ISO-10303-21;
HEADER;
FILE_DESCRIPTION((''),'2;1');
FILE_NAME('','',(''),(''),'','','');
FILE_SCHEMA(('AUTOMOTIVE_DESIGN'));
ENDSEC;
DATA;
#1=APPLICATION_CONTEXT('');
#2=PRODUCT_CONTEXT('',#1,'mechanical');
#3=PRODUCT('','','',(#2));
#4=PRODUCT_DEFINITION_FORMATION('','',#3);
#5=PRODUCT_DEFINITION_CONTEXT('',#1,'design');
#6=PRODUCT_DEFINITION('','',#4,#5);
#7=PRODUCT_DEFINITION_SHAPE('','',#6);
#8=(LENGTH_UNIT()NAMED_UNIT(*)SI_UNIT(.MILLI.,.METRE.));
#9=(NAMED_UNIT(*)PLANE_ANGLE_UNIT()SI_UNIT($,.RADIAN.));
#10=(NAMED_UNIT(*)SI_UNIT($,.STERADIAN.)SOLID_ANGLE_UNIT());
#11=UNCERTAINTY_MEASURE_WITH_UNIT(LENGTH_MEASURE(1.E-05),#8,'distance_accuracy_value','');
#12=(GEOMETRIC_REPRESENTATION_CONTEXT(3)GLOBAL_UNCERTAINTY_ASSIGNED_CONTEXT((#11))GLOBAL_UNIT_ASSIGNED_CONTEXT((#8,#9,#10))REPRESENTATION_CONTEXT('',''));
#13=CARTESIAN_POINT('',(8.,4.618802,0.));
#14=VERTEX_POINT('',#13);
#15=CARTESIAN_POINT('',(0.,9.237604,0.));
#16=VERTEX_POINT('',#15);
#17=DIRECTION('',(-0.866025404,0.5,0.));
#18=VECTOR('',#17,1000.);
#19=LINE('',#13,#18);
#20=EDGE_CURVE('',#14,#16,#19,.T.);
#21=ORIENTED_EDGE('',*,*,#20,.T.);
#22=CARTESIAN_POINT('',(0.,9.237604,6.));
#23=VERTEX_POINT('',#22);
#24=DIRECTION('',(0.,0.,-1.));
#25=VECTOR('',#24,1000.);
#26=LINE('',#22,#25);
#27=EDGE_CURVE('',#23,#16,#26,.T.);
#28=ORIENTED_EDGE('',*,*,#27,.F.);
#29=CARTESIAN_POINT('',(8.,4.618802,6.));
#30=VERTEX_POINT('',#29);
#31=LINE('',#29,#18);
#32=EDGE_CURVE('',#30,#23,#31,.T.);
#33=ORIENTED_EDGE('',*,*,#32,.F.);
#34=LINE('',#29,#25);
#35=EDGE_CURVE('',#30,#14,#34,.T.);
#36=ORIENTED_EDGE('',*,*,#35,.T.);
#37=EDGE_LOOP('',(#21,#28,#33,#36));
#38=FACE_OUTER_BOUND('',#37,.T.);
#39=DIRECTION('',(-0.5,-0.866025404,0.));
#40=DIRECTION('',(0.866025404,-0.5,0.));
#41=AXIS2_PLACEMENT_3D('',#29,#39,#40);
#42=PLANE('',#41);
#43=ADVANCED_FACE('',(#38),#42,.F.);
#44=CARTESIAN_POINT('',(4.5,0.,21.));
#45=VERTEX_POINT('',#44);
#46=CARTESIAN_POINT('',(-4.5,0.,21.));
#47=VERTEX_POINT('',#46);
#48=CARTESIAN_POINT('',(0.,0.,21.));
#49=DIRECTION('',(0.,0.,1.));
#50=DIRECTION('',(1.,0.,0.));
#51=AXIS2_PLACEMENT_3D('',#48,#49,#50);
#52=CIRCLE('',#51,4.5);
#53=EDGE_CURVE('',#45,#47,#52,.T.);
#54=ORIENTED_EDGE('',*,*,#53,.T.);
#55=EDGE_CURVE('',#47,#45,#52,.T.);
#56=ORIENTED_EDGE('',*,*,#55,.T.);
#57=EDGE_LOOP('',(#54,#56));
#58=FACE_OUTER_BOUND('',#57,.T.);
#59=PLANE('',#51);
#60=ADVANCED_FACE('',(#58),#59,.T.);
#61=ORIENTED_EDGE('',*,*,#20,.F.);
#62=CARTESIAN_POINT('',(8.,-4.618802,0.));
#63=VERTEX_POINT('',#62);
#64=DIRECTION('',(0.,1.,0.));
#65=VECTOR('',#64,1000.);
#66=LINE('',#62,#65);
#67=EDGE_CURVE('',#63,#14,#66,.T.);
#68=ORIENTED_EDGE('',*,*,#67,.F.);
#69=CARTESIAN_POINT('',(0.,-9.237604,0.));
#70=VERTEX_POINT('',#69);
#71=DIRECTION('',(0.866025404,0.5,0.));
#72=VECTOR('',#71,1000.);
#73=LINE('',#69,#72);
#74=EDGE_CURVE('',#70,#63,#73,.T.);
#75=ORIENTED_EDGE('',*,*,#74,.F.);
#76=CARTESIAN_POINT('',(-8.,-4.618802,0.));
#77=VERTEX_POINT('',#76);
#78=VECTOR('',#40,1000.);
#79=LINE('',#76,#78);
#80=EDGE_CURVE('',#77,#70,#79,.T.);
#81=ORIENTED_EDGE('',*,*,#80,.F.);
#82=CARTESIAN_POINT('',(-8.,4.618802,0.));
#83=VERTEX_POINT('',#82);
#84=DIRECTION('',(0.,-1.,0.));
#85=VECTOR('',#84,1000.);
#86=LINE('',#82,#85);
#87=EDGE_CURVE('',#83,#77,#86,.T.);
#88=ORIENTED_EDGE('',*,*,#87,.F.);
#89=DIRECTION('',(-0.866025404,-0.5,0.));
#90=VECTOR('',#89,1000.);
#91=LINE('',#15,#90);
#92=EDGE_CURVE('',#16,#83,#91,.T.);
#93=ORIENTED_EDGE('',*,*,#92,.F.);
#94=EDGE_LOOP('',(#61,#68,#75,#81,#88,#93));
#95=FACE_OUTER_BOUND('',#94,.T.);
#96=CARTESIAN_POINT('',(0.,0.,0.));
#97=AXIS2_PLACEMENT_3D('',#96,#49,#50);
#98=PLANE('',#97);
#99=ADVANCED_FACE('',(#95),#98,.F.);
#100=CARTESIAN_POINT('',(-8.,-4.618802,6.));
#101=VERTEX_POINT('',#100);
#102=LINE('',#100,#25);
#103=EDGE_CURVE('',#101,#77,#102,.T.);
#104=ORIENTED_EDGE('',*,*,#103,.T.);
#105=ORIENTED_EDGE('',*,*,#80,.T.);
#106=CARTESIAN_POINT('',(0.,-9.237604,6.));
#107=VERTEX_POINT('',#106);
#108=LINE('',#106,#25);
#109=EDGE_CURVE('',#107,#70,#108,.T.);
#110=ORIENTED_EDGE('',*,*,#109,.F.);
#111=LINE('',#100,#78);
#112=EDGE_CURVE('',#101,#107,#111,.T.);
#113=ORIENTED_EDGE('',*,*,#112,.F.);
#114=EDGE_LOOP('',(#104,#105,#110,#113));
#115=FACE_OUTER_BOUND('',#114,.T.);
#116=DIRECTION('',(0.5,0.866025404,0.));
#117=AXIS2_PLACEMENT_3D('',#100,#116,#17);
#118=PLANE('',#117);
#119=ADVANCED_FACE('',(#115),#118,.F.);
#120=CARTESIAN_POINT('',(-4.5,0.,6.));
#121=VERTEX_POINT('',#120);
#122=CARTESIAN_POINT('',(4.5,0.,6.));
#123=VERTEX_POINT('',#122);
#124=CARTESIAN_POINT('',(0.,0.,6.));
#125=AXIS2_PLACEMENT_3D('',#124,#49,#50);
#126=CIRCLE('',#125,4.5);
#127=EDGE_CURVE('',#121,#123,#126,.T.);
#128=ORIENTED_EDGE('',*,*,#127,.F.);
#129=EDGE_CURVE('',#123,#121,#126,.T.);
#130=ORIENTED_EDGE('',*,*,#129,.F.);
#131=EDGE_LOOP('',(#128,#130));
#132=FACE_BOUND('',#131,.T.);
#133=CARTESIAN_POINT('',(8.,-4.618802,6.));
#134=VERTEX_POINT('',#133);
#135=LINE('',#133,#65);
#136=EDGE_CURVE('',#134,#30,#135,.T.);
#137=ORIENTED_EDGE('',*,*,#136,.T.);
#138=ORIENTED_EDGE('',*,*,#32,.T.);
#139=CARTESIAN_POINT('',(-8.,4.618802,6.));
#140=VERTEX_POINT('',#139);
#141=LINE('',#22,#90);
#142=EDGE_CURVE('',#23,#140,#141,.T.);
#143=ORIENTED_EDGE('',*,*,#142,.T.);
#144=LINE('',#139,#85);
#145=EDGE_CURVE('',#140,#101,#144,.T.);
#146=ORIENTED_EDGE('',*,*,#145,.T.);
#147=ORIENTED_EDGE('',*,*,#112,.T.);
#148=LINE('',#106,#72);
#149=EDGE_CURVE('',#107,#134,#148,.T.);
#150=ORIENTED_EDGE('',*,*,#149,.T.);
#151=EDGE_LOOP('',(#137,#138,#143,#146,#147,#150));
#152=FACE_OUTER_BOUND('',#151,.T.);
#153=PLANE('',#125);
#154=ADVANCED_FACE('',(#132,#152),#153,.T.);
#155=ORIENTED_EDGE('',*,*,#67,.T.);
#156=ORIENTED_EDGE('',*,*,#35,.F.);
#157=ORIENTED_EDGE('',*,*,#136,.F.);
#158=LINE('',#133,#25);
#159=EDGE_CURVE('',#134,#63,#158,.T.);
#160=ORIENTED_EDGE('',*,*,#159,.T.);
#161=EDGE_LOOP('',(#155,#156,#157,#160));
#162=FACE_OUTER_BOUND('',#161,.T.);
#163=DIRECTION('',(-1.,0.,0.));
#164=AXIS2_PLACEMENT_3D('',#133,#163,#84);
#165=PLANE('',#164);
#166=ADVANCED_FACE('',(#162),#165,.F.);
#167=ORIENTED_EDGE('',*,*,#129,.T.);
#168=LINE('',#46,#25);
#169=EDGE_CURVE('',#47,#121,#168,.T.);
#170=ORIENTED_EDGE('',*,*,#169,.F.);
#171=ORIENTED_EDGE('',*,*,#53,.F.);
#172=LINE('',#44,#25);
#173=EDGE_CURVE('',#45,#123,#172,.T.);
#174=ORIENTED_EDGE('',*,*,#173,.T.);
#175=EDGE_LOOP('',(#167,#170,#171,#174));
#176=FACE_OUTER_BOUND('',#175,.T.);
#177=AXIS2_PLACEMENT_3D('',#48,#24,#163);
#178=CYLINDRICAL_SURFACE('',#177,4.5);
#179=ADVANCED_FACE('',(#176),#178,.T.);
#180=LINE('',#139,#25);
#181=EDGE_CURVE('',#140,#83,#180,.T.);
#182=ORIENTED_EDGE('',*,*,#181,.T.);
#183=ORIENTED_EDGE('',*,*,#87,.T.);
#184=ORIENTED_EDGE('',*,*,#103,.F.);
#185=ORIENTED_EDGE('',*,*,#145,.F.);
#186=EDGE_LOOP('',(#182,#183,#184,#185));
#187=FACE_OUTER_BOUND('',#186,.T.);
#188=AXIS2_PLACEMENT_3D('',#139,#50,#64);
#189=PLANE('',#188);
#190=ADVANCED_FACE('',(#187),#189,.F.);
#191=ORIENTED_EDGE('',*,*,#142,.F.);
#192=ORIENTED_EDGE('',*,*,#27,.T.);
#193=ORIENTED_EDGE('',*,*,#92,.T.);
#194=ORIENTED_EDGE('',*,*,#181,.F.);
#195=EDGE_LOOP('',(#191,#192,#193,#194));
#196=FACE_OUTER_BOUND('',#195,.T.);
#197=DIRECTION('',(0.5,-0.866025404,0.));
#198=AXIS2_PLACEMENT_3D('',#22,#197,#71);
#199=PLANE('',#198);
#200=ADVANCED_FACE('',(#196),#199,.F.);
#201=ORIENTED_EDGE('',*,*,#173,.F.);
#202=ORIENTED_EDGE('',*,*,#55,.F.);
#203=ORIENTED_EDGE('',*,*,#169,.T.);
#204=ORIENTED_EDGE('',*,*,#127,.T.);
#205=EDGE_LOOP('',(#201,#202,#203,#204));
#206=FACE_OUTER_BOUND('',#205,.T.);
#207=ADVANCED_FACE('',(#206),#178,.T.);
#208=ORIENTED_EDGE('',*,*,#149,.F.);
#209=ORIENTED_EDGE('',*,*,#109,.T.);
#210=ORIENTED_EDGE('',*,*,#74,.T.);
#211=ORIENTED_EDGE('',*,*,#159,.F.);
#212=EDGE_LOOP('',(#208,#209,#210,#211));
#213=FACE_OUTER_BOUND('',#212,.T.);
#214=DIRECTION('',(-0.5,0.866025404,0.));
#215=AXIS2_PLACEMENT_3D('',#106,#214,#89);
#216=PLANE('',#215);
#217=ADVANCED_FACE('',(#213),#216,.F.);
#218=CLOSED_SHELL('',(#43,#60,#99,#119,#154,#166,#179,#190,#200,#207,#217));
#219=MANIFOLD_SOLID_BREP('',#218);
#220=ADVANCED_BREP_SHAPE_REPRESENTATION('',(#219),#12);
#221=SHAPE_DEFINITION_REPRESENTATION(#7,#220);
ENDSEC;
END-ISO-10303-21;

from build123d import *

# Parameters (mm, degrees)
BOSS_EXTRUDE2_DEPTH = 6
SKETCH3_R           = 4.5
BOSS_EXTRUDE3_DEPTH = 15


with BuildPart() as part:
    # Sketch2 → Boss-Extrude2 (new body)
    with BuildSketch(Plane.XY):
        Polygon((0, 9.237604307), (-8, 4.618802154), (-8, -4.618802154), (0, -9.237604307), (8, -4.618802154), (8, 4.618802154), align=None)
    extrude(amount=BOSS_EXTRUDE2_DEPTH)

    # Sketch3 → Boss-Extrude3 (add)
    with BuildSketch(Plane.XY.offset(6)):
        Circle(SKETCH3_R)
    extrude(amount=BOSS_EXTRUDE3_DEPTH)


solid = part.part
